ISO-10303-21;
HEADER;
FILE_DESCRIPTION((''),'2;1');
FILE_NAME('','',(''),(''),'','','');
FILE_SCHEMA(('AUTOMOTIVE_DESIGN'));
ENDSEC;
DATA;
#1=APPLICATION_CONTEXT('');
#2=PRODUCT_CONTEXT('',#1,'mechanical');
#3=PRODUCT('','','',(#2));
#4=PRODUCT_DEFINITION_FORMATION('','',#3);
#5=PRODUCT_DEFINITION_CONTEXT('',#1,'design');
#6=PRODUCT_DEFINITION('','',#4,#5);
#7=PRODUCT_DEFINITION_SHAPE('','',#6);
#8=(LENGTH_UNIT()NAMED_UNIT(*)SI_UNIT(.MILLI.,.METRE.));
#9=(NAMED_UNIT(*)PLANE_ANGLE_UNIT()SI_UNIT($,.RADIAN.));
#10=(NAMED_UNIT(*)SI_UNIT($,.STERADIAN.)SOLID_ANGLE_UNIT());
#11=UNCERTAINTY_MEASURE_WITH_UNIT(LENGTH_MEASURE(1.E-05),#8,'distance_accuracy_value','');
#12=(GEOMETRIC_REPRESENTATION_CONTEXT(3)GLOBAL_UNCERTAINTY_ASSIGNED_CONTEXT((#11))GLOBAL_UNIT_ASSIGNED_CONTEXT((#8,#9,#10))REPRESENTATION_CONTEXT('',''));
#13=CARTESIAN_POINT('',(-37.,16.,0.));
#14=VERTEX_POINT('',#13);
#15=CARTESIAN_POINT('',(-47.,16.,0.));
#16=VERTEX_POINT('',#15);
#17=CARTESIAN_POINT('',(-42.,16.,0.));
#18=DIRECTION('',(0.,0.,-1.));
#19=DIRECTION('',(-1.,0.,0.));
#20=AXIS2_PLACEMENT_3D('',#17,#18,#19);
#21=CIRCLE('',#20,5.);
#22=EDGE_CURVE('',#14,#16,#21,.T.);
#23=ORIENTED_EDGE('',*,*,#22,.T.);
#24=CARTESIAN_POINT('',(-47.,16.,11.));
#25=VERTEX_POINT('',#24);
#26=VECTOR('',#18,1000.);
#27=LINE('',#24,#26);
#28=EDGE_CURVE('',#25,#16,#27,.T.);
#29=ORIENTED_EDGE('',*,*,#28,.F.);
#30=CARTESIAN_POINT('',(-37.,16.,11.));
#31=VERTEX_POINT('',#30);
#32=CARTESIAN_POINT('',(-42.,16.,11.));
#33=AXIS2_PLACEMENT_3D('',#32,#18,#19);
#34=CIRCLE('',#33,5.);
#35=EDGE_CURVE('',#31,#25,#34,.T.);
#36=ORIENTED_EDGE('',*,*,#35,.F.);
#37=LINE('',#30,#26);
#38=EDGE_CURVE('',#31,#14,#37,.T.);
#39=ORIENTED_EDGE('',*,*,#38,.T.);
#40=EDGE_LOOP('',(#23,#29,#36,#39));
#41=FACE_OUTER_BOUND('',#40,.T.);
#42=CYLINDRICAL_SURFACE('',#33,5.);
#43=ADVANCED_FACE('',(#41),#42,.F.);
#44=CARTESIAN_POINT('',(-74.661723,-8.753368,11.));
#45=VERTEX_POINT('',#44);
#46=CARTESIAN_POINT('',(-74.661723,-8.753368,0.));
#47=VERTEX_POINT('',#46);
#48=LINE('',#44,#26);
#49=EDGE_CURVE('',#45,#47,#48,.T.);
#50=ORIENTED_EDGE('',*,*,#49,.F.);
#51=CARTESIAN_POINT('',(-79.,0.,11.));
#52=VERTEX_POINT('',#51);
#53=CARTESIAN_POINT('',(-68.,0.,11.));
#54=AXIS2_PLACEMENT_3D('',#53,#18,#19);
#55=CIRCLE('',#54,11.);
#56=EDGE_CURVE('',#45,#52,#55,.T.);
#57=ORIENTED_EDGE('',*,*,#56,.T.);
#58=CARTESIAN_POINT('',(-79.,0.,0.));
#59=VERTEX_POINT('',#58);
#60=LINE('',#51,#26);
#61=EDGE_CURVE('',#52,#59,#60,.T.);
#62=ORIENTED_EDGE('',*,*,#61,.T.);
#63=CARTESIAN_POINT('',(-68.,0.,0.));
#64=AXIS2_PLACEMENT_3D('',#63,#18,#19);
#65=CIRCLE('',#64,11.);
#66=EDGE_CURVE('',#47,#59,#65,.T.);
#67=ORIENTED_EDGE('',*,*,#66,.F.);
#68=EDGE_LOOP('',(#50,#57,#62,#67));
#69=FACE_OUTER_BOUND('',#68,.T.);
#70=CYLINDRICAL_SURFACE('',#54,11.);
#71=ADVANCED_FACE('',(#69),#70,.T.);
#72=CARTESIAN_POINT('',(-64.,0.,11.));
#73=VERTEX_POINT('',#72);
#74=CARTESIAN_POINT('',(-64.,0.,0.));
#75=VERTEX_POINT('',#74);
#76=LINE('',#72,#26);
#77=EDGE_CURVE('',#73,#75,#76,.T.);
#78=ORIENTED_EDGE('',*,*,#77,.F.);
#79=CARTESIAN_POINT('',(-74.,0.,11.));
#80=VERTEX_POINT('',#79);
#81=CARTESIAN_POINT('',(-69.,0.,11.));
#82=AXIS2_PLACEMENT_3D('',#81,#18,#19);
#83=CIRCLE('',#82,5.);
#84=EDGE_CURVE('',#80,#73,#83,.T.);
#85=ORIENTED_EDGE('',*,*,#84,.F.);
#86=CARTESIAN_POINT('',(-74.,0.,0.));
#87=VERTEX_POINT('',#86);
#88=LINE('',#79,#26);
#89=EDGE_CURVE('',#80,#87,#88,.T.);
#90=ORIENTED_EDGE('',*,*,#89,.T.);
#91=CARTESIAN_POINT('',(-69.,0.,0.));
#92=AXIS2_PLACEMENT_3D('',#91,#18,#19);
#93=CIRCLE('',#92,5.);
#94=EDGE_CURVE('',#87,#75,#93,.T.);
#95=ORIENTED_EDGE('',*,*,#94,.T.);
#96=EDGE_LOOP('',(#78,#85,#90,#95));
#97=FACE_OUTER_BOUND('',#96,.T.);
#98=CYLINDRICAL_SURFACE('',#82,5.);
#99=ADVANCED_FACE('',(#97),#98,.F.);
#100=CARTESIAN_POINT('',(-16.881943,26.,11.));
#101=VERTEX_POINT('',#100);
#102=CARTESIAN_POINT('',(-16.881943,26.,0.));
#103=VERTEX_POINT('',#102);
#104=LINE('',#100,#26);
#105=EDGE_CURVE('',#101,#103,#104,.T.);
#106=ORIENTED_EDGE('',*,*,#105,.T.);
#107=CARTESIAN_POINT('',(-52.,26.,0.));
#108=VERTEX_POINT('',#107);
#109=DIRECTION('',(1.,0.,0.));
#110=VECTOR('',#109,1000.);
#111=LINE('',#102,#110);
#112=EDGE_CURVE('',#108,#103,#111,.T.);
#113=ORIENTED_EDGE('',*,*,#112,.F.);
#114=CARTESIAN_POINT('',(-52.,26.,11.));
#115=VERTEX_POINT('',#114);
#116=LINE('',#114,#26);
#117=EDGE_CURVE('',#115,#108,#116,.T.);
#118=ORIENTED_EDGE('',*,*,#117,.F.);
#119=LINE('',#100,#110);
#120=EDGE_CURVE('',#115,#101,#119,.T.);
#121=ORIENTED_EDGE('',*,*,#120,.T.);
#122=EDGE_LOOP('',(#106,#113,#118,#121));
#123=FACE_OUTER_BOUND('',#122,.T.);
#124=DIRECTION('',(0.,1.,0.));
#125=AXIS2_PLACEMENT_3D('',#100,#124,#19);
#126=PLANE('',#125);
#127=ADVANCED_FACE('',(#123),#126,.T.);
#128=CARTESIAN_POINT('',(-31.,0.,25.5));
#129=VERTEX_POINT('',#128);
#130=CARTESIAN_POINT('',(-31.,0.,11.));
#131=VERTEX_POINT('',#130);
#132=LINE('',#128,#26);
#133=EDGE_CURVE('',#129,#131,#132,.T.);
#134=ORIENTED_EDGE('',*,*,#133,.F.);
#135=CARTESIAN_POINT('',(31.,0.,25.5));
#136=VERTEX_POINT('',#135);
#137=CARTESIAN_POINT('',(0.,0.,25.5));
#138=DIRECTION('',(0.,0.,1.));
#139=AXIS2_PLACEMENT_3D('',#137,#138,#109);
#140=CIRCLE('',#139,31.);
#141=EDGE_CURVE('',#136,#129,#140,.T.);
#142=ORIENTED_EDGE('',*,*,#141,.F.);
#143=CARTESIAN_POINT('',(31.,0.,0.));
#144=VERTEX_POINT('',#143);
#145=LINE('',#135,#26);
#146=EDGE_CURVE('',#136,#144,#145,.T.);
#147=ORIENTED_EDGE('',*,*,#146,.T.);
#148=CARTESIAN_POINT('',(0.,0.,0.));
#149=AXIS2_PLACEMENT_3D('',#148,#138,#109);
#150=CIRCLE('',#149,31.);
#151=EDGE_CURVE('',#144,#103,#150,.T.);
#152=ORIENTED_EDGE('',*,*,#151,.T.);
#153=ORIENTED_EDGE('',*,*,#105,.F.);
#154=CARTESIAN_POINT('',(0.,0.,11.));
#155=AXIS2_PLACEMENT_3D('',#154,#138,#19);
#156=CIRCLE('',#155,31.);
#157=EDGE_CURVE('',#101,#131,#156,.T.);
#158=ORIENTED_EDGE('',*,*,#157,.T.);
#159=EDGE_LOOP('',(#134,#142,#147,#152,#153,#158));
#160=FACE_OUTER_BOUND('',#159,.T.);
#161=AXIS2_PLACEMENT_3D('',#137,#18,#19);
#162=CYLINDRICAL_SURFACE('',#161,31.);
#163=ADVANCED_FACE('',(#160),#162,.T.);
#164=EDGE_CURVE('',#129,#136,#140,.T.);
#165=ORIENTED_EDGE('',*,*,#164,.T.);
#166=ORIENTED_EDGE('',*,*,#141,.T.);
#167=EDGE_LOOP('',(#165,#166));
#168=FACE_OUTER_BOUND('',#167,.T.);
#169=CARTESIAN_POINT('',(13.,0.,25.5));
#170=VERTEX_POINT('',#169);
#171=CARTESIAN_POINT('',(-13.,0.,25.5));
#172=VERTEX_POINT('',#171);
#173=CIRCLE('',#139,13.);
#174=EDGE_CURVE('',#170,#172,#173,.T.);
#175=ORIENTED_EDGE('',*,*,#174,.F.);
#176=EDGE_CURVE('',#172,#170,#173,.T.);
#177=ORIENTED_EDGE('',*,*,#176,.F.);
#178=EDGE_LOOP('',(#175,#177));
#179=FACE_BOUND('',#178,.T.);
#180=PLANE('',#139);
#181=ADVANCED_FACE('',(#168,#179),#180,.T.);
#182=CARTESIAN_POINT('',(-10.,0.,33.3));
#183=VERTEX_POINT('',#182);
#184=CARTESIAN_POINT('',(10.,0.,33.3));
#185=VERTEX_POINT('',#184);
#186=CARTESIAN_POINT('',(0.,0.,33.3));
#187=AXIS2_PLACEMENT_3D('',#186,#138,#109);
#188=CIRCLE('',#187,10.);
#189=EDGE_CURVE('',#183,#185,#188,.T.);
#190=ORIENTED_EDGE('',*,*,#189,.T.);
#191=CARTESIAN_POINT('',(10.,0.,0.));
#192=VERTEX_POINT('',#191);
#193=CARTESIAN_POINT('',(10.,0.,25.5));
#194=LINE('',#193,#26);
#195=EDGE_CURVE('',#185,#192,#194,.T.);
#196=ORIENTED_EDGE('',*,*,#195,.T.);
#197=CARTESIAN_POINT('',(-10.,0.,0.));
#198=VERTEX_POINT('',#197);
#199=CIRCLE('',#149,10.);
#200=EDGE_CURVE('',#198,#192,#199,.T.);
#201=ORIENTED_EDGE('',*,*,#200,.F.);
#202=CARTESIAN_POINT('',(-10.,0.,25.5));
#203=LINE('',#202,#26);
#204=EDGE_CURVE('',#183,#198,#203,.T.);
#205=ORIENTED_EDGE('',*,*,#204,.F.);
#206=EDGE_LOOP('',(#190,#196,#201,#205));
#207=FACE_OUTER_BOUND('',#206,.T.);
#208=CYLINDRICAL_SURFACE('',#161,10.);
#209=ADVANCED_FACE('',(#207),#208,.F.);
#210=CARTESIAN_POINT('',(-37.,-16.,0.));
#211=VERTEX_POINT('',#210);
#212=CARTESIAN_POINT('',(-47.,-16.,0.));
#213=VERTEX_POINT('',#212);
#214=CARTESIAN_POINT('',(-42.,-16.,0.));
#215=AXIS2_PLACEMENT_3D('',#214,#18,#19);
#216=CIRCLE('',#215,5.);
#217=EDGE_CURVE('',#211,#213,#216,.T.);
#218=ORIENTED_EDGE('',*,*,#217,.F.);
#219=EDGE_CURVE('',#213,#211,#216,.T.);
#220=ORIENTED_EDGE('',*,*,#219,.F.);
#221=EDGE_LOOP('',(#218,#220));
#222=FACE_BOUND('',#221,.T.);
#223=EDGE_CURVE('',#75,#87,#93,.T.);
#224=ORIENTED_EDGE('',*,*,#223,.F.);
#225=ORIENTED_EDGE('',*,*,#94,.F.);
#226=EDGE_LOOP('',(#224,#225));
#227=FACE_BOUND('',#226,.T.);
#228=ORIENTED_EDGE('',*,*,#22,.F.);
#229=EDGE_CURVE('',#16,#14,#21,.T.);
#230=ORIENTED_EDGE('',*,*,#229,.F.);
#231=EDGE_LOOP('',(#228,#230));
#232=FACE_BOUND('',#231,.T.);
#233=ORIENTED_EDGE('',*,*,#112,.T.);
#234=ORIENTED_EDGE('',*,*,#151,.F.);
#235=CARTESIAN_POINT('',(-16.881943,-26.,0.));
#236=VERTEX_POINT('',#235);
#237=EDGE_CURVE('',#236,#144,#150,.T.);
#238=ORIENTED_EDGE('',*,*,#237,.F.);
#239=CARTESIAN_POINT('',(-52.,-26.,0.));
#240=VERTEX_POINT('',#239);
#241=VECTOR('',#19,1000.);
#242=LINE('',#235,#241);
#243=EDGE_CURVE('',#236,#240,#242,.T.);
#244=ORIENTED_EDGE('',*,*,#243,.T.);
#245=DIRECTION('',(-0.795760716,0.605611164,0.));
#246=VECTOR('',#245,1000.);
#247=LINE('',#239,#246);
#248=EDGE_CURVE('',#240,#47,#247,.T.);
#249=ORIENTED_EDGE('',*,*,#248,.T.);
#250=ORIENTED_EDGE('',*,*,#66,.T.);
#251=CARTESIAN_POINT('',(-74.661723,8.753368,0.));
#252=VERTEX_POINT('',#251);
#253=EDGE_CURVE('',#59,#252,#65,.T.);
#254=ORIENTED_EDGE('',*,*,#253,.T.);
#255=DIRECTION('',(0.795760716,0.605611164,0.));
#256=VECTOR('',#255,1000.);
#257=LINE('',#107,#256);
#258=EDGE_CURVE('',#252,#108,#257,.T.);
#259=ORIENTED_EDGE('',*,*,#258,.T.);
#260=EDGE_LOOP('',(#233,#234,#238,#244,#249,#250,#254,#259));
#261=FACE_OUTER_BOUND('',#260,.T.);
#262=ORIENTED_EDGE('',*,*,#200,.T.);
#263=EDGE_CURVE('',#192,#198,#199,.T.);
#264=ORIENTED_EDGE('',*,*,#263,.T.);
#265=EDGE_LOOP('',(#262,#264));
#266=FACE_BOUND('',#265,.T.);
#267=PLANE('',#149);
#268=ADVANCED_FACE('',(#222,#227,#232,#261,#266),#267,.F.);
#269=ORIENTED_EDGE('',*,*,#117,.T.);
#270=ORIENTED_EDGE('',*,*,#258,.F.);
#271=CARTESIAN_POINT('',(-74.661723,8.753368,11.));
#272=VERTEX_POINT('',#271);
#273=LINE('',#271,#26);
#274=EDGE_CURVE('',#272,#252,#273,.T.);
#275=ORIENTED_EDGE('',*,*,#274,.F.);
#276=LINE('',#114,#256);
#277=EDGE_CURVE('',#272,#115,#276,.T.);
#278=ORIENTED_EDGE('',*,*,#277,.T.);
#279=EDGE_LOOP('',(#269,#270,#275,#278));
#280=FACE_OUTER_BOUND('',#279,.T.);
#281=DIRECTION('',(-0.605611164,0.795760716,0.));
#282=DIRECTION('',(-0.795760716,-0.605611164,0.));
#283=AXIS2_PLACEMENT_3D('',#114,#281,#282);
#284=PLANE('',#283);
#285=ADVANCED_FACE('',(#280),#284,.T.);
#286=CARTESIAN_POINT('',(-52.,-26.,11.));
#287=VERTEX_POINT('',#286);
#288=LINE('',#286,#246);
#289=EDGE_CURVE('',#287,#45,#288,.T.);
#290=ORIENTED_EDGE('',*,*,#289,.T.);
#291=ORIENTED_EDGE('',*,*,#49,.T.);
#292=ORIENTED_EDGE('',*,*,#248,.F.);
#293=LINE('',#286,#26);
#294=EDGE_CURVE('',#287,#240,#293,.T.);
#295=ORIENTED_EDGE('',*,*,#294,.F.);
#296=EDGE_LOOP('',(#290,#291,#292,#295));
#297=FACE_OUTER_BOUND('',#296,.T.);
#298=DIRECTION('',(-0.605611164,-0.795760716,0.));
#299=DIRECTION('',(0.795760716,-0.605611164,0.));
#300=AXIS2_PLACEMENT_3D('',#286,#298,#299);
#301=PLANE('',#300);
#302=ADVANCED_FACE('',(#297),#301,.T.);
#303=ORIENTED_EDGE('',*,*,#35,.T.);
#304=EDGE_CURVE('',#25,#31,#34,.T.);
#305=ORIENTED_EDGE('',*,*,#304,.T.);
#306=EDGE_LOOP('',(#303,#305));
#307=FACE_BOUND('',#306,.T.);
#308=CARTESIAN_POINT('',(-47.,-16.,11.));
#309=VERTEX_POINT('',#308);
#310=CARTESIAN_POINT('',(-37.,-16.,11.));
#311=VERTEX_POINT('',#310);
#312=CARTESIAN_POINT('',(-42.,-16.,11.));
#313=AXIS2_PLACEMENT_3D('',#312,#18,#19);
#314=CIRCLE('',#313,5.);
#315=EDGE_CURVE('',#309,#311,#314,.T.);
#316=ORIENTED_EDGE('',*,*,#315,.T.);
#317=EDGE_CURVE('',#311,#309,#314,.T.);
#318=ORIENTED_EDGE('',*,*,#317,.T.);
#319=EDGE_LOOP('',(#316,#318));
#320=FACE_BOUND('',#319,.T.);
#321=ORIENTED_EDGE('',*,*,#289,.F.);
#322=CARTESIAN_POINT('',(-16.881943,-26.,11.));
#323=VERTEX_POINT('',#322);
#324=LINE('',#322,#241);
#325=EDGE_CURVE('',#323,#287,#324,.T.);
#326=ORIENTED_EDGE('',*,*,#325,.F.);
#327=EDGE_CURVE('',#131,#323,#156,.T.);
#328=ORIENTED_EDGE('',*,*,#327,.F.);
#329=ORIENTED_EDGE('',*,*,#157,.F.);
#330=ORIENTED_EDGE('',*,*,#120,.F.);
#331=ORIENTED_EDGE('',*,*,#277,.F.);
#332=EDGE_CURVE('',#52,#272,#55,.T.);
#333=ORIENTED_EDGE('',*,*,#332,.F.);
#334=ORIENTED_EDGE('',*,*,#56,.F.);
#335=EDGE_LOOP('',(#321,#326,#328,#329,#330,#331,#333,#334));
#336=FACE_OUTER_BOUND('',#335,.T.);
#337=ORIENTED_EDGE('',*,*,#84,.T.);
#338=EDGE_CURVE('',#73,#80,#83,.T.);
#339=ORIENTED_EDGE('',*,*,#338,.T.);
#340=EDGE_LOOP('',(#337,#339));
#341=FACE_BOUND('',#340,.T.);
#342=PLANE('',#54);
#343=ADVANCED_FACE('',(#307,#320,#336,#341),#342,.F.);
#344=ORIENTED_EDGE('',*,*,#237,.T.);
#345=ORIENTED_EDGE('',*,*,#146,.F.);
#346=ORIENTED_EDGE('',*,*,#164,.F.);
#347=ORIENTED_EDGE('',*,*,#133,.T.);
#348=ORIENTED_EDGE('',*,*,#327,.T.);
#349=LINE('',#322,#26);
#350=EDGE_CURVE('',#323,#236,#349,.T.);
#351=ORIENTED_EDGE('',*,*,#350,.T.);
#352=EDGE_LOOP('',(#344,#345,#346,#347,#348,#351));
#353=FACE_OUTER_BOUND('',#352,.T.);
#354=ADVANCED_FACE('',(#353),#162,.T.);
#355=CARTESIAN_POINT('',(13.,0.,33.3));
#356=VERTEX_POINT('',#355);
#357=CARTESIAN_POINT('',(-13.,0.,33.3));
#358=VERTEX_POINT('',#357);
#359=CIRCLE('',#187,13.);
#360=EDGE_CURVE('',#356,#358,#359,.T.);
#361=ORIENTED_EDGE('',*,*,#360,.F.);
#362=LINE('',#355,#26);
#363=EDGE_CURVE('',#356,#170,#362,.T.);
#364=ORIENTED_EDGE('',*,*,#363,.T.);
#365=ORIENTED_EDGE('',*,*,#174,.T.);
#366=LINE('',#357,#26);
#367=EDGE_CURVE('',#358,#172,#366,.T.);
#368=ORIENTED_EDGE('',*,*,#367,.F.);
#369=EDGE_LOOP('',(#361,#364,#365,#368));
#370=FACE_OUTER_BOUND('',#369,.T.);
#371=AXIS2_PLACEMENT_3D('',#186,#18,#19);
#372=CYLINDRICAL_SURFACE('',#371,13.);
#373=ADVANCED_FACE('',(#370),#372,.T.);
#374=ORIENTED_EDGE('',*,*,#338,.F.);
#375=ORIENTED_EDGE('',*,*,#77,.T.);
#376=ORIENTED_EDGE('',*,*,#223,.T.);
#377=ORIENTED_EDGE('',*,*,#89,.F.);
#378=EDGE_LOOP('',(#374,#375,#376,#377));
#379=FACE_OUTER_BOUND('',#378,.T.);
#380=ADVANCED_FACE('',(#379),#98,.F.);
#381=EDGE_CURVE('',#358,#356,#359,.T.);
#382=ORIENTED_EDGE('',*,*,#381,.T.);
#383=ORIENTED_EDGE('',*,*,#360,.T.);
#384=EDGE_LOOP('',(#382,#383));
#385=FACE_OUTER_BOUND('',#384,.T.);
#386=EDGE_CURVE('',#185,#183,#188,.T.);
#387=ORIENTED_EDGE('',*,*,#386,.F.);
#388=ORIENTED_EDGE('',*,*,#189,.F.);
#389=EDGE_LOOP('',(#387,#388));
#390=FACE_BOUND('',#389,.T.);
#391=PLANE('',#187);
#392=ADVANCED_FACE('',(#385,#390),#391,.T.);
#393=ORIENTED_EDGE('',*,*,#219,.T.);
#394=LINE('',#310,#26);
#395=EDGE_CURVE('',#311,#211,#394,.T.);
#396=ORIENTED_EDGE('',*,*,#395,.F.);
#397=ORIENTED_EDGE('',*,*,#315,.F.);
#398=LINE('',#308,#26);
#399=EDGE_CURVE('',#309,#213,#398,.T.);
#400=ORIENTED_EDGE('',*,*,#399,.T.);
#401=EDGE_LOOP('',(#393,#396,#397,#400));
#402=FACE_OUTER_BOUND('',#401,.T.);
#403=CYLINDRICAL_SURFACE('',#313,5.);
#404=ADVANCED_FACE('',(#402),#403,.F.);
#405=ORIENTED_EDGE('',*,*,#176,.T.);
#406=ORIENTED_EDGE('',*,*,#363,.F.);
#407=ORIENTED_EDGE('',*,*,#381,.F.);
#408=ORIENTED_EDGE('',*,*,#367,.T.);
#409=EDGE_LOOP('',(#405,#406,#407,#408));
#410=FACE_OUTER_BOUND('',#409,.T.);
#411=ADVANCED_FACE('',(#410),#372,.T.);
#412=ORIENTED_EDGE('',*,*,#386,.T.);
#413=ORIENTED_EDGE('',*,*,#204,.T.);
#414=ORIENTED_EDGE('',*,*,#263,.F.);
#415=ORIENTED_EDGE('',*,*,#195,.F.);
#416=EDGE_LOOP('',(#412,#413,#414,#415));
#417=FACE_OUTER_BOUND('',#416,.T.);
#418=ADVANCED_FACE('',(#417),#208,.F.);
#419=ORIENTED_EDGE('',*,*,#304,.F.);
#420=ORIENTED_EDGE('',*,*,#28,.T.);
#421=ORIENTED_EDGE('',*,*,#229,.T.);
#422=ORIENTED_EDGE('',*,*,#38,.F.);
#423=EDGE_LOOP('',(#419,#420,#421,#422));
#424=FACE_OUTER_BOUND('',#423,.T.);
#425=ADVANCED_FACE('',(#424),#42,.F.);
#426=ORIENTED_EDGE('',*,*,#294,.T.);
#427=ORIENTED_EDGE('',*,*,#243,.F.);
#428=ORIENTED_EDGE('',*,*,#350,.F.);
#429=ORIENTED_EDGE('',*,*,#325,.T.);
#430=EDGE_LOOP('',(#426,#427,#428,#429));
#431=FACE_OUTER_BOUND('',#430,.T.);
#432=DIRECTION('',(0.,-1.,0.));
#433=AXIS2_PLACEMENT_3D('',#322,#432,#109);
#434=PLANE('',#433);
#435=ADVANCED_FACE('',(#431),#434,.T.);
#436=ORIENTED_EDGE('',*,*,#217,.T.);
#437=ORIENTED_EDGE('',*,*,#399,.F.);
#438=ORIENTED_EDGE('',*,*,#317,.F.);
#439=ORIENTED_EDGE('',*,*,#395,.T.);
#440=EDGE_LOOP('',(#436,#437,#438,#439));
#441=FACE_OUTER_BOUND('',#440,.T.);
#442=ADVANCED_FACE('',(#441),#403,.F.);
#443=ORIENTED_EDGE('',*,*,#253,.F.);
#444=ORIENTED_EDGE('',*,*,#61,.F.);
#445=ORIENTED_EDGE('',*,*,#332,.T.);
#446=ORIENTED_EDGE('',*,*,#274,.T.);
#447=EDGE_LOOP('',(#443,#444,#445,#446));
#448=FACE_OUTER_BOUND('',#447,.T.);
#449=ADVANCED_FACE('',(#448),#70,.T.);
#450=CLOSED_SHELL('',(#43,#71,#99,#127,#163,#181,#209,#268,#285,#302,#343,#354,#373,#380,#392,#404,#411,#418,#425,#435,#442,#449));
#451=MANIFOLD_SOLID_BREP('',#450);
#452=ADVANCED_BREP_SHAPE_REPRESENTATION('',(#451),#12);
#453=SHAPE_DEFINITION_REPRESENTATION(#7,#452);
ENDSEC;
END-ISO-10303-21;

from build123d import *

# Parameters (mm, degrees)
SKETCH_1_R      = 31
SKETCH_1_R_2    = 10
EXTRUDE_1_DEPTH = 25.5
SKETCH_2_R      = 5
EXTRUDE_2_DEPTH = 11
SKETCH_3_R      = 13
SKETCH_3_R_2    = 10
EXTRUDE_3_DEPTH = 7.8


with BuildPart() as part:
    # 草图1 → 凸台-拉伸1 (new body)
    with BuildSketch(Plane.XY):
        Circle(SKETCH_1_R)
        Circle(SKETCH_1_R_2, mode=Mode.SUBTRACT)
    extrude(amount=EXTRUDE_1_DEPTH)

    # 草图2 → 凸台-拉伸2 (add)
    with BuildSketch(Plane(origin=(0, 0, 0), x_dir=(-1, 0, 0), z_dir=(0, 0, -1))):
        with BuildLine():
            Line((16.881943016, 26), (52, 26))
            Line((52, 26), (74.661722806, 8.753367881))
            ThreePointArc((74.661722806, 8.753367881), (79, 0), (74.661722806, -8.753367881))
            Line((74.661722806, -8.753367881), (52, -26))
            Line((52, -26), (16.881943016, -26))
            ThreePointArc((16.881943016, -26), (31, 0), (16.881943016, 26))
        make_face()
        with Locations((69, 0)):
            Circle(SKETCH_2_R, mode=Mode.SUBTRACT)
        with Locations((42, 16)):
            Circle(SKETCH_2_R, mode=Mode.SUBTRACT)
        with Locations((42, -16)):
            Circle(SKETCH_2_R, mode=Mode.SUBTRACT)
    extrude(amount=-EXTRUDE_2_DEPTH)

    # 草图3 → 凸台-拉伸3 (add)
    with BuildSketch(Plane.XY.offset(25.5)):
        Circle(SKETCH_3_R)
        Circle(SKETCH_3_R_2, mode=Mode.SUBTRACT)
    extrude(amount=EXTRUDE_3_DEPTH)


solid = part.part
